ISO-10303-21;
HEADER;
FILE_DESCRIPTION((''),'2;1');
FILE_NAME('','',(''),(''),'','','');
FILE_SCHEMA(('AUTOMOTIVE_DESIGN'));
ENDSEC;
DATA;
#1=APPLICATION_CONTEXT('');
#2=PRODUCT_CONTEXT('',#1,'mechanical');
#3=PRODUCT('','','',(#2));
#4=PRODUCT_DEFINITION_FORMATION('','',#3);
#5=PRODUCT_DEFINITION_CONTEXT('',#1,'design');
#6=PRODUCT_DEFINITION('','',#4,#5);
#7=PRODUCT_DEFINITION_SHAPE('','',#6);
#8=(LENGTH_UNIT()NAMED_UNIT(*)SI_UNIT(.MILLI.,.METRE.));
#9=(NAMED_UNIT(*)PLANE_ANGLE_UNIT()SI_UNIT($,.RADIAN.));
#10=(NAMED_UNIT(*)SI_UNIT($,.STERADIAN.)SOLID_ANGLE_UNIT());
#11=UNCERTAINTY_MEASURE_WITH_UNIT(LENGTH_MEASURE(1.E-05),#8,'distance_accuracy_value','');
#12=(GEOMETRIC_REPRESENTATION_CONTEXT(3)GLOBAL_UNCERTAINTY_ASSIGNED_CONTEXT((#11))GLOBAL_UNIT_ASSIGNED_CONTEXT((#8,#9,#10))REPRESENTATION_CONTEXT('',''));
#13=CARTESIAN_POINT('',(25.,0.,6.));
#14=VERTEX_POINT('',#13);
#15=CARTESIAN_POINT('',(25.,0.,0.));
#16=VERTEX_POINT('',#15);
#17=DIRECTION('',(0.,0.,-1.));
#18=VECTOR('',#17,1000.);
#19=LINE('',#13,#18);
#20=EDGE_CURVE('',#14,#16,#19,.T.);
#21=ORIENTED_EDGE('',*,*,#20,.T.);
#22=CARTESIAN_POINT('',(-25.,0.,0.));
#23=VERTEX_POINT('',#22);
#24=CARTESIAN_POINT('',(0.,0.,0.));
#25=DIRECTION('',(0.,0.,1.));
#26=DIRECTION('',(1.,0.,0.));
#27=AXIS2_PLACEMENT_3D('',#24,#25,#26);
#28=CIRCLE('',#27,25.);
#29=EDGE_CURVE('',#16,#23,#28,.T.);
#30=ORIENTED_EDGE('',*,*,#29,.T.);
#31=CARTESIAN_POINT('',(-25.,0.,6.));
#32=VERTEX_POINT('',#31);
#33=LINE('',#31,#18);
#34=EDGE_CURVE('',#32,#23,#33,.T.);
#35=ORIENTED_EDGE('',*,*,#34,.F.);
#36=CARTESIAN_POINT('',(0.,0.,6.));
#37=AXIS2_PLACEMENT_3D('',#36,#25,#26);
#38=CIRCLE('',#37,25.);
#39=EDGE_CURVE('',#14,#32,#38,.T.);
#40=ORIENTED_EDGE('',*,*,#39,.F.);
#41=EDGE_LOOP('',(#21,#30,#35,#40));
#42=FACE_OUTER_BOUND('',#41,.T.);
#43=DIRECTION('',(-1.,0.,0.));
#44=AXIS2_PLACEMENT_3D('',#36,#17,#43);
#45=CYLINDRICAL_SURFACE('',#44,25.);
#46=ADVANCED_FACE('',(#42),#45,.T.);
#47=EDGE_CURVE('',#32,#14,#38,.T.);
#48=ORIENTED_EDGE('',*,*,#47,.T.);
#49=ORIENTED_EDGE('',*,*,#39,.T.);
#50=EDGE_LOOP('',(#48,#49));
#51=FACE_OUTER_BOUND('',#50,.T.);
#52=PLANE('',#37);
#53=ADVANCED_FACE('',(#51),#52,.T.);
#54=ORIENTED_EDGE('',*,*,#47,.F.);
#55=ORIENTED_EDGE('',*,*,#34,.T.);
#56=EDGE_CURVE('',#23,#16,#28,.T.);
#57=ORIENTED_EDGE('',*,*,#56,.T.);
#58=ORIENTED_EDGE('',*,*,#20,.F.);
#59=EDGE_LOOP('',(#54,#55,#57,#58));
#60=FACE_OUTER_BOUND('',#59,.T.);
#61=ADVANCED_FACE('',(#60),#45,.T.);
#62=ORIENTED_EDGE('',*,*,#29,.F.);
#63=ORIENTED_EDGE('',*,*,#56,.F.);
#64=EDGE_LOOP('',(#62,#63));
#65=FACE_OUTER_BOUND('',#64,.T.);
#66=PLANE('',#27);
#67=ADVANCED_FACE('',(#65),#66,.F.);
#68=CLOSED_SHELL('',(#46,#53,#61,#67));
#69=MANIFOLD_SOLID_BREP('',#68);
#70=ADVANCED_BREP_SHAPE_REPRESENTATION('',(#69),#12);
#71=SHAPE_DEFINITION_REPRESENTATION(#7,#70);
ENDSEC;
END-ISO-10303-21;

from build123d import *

# Parameters (mm, degrees)
SKETCH_1_R      = 25
EXTRUDE_1_DEPTH = 6


with BuildPart() as part:
    # 草图1 → 凸台-拉伸1 (new body)
    with BuildSketch(Plane.XY):
        Circle(SKETCH_1_R)
    extrude(amount=EXTRUDE_1_DEPTH)


solid = part.part
